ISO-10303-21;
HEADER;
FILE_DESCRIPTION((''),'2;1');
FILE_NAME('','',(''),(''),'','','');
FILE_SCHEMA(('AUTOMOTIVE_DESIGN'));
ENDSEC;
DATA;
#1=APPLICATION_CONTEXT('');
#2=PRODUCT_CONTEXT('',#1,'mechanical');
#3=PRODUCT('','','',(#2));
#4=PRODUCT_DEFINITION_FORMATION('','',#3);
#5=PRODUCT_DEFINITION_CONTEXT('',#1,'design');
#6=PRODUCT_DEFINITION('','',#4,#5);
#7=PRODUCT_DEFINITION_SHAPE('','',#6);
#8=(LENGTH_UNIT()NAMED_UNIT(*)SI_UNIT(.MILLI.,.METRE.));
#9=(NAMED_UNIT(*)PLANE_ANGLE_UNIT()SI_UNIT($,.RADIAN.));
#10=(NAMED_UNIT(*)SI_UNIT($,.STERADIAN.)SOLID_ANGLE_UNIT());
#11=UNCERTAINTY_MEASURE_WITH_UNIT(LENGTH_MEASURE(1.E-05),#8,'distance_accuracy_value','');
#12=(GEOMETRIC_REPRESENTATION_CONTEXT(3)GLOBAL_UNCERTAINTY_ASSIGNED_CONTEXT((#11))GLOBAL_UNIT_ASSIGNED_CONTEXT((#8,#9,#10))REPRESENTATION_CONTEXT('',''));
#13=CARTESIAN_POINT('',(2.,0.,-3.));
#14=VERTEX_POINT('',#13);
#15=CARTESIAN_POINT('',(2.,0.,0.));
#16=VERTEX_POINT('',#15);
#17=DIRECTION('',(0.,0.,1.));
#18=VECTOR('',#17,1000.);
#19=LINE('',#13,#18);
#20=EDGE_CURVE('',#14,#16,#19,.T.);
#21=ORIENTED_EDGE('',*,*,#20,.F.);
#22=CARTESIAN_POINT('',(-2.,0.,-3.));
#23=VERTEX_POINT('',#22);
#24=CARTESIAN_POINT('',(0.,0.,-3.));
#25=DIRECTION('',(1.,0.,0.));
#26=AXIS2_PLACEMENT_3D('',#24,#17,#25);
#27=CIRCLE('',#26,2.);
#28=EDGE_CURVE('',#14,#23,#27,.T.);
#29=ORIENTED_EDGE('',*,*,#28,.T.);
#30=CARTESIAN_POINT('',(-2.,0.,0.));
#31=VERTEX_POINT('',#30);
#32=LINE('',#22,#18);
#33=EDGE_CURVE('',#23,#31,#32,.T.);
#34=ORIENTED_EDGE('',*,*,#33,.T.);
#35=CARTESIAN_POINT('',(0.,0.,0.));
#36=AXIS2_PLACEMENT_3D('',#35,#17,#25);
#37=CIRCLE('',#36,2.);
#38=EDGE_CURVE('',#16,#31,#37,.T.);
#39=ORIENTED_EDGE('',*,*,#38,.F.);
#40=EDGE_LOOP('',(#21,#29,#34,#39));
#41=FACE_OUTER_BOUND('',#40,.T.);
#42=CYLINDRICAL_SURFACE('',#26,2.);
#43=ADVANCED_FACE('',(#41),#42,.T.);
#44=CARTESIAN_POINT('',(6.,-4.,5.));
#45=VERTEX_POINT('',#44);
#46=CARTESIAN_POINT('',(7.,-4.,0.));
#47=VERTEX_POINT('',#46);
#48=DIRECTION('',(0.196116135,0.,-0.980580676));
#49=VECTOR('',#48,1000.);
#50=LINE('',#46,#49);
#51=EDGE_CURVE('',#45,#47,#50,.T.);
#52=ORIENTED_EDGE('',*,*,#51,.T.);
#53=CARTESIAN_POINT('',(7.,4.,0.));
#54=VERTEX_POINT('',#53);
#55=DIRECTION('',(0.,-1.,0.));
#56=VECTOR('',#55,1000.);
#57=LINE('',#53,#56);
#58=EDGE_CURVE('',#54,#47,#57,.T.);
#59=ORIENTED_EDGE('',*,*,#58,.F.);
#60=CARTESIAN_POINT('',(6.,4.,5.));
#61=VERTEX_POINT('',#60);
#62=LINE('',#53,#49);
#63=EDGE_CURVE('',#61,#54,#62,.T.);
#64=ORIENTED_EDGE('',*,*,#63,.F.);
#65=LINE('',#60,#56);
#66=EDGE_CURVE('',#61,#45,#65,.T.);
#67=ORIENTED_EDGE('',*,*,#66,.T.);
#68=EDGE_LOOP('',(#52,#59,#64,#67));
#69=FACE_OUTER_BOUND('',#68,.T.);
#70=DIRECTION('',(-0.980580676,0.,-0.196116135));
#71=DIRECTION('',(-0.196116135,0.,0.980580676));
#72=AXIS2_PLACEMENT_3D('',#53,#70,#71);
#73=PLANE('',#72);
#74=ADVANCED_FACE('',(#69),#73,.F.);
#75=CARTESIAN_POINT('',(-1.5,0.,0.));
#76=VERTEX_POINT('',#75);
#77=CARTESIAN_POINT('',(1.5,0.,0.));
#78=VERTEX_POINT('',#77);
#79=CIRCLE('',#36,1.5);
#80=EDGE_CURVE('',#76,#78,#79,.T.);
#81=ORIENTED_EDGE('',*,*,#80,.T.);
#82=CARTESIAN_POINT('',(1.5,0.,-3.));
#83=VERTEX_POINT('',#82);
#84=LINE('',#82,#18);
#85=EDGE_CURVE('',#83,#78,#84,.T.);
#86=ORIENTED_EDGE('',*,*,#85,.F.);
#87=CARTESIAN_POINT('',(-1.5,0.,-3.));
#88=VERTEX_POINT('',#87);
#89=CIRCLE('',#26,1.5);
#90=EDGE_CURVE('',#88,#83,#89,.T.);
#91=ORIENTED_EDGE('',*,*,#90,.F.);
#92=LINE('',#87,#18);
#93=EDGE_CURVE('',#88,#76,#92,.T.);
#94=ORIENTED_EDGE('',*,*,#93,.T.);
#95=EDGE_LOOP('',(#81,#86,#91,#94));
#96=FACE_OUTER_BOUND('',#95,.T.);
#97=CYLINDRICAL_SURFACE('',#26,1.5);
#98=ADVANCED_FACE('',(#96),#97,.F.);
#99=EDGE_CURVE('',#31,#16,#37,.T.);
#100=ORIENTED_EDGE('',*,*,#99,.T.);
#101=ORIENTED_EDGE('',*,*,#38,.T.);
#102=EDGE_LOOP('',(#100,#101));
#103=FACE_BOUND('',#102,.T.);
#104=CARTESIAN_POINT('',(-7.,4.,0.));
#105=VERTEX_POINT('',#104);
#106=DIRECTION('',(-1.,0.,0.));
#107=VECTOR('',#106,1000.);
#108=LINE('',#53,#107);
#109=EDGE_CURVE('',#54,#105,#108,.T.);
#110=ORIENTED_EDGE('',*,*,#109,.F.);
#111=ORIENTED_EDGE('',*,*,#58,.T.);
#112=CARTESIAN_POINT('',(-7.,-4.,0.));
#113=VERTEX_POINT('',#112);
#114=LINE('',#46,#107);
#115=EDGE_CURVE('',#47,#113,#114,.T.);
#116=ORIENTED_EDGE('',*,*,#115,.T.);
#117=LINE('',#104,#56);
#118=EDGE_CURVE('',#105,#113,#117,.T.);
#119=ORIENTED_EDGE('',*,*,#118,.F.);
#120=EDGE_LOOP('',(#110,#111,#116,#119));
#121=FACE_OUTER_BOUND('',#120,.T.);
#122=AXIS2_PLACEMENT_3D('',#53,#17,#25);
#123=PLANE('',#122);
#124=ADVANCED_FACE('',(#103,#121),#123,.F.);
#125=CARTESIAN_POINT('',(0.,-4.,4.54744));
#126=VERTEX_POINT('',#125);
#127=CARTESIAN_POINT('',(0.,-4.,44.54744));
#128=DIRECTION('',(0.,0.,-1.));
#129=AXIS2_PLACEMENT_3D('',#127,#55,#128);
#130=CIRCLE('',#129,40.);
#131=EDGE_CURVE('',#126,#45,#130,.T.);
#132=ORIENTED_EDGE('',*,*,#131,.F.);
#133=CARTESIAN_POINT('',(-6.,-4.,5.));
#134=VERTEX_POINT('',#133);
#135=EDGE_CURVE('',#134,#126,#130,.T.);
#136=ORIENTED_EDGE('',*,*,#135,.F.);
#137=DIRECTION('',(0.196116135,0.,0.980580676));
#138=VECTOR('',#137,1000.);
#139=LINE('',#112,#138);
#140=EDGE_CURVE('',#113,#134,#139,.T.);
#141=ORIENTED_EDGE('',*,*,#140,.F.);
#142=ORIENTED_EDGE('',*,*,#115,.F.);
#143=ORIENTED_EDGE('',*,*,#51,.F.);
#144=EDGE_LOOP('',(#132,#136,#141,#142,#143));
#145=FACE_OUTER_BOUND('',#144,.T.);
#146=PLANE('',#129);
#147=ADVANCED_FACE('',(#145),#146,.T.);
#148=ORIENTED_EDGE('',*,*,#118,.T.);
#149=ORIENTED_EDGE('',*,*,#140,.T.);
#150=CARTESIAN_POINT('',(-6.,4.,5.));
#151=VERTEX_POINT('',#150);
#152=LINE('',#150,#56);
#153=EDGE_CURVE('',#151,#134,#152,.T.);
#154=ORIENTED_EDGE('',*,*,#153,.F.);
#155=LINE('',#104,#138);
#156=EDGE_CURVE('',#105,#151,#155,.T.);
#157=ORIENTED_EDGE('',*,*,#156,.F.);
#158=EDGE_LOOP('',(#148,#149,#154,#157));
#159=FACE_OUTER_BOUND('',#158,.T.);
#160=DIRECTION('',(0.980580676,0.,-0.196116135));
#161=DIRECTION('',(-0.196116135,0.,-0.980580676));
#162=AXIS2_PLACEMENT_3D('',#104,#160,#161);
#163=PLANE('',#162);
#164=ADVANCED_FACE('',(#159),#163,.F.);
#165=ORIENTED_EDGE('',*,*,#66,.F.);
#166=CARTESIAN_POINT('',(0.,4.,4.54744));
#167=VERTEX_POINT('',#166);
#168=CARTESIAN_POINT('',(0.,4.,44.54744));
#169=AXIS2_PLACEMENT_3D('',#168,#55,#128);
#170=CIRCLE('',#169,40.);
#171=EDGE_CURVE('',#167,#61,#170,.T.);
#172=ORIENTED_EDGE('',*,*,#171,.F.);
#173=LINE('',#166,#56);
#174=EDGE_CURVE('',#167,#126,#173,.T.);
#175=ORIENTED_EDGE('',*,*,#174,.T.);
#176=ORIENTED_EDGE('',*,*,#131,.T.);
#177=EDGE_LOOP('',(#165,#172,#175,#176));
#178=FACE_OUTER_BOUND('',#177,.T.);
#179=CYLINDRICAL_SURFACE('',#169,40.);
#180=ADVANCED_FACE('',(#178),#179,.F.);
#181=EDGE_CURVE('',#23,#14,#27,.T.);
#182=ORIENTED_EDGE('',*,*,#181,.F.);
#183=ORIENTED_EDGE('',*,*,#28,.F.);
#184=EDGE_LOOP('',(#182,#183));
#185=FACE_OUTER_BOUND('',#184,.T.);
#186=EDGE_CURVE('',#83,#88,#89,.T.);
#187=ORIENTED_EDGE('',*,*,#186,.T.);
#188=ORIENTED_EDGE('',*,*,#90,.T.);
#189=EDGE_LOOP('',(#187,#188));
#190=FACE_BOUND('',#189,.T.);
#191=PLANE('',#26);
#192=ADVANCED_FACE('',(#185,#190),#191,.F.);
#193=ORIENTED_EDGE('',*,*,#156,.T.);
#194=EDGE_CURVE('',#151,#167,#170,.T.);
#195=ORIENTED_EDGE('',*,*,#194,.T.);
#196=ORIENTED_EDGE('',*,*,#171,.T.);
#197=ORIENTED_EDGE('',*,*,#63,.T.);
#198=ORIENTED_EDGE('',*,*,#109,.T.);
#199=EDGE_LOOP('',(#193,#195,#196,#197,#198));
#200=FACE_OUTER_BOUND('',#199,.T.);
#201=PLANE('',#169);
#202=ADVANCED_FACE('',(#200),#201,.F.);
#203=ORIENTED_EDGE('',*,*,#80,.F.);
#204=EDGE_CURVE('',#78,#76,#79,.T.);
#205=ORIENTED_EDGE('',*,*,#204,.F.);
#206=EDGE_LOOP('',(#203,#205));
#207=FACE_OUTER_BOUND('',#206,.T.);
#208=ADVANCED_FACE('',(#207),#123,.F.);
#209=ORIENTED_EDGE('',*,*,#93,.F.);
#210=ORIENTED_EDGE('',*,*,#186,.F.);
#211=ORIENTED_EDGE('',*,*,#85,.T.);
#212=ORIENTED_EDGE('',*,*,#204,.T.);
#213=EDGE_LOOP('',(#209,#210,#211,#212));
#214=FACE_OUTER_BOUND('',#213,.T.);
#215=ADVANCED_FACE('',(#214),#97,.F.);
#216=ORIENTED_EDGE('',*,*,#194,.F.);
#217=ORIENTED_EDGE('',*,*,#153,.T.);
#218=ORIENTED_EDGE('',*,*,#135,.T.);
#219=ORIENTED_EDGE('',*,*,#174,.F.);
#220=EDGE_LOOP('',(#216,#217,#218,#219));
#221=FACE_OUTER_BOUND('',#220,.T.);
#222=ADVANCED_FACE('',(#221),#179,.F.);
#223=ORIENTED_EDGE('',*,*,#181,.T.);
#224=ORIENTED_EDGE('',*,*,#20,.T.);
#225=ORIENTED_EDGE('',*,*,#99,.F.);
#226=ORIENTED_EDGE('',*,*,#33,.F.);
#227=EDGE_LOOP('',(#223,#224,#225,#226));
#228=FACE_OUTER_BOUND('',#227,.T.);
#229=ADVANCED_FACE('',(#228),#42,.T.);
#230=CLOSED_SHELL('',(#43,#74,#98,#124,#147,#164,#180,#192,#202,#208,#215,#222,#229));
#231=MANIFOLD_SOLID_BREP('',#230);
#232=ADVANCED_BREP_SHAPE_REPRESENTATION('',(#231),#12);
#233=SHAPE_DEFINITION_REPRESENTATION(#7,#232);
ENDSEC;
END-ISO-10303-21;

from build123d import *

# Parameters (mm, degrees)
BOSS_EXTRUDE1_DEPTH = 4
SKETCH2_R           = 2
SKETCH2_R_2         = 1.5
BOSS_EXTRUDE2_DEPTH = 3


with BuildPart() as part:
    # Sketch1 → Boss-Extrude1 (new, symmetric)
    with BuildSketch(Plane(origin=(0, 0, 0), x_dir=(1, 0, 0), z_dir=(0, 1, 0))):
        with BuildLine():
            Line((7, 0), (-7, 0))
            Line((-7, 0), (-6, -5))
            ThreePointArc((-6, -5), (0, -4.547439867), (6, -5))
            Line((6, -5), (7, 0))
        make_face()
    extrude(amount=BOSS_EXTRUDE1_DEPTH, both=True)

    # Sketch2 → Boss-Extrude2 (add)
    with BuildSketch(Plane.XY):
        Circle(SKETCH2_R)
        Circle(SKETCH2_R_2, mode=Mode.SUBTRACT)
    extrude(amount=-BOSS_EXTRUDE2_DEPTH)


solid = part.part
